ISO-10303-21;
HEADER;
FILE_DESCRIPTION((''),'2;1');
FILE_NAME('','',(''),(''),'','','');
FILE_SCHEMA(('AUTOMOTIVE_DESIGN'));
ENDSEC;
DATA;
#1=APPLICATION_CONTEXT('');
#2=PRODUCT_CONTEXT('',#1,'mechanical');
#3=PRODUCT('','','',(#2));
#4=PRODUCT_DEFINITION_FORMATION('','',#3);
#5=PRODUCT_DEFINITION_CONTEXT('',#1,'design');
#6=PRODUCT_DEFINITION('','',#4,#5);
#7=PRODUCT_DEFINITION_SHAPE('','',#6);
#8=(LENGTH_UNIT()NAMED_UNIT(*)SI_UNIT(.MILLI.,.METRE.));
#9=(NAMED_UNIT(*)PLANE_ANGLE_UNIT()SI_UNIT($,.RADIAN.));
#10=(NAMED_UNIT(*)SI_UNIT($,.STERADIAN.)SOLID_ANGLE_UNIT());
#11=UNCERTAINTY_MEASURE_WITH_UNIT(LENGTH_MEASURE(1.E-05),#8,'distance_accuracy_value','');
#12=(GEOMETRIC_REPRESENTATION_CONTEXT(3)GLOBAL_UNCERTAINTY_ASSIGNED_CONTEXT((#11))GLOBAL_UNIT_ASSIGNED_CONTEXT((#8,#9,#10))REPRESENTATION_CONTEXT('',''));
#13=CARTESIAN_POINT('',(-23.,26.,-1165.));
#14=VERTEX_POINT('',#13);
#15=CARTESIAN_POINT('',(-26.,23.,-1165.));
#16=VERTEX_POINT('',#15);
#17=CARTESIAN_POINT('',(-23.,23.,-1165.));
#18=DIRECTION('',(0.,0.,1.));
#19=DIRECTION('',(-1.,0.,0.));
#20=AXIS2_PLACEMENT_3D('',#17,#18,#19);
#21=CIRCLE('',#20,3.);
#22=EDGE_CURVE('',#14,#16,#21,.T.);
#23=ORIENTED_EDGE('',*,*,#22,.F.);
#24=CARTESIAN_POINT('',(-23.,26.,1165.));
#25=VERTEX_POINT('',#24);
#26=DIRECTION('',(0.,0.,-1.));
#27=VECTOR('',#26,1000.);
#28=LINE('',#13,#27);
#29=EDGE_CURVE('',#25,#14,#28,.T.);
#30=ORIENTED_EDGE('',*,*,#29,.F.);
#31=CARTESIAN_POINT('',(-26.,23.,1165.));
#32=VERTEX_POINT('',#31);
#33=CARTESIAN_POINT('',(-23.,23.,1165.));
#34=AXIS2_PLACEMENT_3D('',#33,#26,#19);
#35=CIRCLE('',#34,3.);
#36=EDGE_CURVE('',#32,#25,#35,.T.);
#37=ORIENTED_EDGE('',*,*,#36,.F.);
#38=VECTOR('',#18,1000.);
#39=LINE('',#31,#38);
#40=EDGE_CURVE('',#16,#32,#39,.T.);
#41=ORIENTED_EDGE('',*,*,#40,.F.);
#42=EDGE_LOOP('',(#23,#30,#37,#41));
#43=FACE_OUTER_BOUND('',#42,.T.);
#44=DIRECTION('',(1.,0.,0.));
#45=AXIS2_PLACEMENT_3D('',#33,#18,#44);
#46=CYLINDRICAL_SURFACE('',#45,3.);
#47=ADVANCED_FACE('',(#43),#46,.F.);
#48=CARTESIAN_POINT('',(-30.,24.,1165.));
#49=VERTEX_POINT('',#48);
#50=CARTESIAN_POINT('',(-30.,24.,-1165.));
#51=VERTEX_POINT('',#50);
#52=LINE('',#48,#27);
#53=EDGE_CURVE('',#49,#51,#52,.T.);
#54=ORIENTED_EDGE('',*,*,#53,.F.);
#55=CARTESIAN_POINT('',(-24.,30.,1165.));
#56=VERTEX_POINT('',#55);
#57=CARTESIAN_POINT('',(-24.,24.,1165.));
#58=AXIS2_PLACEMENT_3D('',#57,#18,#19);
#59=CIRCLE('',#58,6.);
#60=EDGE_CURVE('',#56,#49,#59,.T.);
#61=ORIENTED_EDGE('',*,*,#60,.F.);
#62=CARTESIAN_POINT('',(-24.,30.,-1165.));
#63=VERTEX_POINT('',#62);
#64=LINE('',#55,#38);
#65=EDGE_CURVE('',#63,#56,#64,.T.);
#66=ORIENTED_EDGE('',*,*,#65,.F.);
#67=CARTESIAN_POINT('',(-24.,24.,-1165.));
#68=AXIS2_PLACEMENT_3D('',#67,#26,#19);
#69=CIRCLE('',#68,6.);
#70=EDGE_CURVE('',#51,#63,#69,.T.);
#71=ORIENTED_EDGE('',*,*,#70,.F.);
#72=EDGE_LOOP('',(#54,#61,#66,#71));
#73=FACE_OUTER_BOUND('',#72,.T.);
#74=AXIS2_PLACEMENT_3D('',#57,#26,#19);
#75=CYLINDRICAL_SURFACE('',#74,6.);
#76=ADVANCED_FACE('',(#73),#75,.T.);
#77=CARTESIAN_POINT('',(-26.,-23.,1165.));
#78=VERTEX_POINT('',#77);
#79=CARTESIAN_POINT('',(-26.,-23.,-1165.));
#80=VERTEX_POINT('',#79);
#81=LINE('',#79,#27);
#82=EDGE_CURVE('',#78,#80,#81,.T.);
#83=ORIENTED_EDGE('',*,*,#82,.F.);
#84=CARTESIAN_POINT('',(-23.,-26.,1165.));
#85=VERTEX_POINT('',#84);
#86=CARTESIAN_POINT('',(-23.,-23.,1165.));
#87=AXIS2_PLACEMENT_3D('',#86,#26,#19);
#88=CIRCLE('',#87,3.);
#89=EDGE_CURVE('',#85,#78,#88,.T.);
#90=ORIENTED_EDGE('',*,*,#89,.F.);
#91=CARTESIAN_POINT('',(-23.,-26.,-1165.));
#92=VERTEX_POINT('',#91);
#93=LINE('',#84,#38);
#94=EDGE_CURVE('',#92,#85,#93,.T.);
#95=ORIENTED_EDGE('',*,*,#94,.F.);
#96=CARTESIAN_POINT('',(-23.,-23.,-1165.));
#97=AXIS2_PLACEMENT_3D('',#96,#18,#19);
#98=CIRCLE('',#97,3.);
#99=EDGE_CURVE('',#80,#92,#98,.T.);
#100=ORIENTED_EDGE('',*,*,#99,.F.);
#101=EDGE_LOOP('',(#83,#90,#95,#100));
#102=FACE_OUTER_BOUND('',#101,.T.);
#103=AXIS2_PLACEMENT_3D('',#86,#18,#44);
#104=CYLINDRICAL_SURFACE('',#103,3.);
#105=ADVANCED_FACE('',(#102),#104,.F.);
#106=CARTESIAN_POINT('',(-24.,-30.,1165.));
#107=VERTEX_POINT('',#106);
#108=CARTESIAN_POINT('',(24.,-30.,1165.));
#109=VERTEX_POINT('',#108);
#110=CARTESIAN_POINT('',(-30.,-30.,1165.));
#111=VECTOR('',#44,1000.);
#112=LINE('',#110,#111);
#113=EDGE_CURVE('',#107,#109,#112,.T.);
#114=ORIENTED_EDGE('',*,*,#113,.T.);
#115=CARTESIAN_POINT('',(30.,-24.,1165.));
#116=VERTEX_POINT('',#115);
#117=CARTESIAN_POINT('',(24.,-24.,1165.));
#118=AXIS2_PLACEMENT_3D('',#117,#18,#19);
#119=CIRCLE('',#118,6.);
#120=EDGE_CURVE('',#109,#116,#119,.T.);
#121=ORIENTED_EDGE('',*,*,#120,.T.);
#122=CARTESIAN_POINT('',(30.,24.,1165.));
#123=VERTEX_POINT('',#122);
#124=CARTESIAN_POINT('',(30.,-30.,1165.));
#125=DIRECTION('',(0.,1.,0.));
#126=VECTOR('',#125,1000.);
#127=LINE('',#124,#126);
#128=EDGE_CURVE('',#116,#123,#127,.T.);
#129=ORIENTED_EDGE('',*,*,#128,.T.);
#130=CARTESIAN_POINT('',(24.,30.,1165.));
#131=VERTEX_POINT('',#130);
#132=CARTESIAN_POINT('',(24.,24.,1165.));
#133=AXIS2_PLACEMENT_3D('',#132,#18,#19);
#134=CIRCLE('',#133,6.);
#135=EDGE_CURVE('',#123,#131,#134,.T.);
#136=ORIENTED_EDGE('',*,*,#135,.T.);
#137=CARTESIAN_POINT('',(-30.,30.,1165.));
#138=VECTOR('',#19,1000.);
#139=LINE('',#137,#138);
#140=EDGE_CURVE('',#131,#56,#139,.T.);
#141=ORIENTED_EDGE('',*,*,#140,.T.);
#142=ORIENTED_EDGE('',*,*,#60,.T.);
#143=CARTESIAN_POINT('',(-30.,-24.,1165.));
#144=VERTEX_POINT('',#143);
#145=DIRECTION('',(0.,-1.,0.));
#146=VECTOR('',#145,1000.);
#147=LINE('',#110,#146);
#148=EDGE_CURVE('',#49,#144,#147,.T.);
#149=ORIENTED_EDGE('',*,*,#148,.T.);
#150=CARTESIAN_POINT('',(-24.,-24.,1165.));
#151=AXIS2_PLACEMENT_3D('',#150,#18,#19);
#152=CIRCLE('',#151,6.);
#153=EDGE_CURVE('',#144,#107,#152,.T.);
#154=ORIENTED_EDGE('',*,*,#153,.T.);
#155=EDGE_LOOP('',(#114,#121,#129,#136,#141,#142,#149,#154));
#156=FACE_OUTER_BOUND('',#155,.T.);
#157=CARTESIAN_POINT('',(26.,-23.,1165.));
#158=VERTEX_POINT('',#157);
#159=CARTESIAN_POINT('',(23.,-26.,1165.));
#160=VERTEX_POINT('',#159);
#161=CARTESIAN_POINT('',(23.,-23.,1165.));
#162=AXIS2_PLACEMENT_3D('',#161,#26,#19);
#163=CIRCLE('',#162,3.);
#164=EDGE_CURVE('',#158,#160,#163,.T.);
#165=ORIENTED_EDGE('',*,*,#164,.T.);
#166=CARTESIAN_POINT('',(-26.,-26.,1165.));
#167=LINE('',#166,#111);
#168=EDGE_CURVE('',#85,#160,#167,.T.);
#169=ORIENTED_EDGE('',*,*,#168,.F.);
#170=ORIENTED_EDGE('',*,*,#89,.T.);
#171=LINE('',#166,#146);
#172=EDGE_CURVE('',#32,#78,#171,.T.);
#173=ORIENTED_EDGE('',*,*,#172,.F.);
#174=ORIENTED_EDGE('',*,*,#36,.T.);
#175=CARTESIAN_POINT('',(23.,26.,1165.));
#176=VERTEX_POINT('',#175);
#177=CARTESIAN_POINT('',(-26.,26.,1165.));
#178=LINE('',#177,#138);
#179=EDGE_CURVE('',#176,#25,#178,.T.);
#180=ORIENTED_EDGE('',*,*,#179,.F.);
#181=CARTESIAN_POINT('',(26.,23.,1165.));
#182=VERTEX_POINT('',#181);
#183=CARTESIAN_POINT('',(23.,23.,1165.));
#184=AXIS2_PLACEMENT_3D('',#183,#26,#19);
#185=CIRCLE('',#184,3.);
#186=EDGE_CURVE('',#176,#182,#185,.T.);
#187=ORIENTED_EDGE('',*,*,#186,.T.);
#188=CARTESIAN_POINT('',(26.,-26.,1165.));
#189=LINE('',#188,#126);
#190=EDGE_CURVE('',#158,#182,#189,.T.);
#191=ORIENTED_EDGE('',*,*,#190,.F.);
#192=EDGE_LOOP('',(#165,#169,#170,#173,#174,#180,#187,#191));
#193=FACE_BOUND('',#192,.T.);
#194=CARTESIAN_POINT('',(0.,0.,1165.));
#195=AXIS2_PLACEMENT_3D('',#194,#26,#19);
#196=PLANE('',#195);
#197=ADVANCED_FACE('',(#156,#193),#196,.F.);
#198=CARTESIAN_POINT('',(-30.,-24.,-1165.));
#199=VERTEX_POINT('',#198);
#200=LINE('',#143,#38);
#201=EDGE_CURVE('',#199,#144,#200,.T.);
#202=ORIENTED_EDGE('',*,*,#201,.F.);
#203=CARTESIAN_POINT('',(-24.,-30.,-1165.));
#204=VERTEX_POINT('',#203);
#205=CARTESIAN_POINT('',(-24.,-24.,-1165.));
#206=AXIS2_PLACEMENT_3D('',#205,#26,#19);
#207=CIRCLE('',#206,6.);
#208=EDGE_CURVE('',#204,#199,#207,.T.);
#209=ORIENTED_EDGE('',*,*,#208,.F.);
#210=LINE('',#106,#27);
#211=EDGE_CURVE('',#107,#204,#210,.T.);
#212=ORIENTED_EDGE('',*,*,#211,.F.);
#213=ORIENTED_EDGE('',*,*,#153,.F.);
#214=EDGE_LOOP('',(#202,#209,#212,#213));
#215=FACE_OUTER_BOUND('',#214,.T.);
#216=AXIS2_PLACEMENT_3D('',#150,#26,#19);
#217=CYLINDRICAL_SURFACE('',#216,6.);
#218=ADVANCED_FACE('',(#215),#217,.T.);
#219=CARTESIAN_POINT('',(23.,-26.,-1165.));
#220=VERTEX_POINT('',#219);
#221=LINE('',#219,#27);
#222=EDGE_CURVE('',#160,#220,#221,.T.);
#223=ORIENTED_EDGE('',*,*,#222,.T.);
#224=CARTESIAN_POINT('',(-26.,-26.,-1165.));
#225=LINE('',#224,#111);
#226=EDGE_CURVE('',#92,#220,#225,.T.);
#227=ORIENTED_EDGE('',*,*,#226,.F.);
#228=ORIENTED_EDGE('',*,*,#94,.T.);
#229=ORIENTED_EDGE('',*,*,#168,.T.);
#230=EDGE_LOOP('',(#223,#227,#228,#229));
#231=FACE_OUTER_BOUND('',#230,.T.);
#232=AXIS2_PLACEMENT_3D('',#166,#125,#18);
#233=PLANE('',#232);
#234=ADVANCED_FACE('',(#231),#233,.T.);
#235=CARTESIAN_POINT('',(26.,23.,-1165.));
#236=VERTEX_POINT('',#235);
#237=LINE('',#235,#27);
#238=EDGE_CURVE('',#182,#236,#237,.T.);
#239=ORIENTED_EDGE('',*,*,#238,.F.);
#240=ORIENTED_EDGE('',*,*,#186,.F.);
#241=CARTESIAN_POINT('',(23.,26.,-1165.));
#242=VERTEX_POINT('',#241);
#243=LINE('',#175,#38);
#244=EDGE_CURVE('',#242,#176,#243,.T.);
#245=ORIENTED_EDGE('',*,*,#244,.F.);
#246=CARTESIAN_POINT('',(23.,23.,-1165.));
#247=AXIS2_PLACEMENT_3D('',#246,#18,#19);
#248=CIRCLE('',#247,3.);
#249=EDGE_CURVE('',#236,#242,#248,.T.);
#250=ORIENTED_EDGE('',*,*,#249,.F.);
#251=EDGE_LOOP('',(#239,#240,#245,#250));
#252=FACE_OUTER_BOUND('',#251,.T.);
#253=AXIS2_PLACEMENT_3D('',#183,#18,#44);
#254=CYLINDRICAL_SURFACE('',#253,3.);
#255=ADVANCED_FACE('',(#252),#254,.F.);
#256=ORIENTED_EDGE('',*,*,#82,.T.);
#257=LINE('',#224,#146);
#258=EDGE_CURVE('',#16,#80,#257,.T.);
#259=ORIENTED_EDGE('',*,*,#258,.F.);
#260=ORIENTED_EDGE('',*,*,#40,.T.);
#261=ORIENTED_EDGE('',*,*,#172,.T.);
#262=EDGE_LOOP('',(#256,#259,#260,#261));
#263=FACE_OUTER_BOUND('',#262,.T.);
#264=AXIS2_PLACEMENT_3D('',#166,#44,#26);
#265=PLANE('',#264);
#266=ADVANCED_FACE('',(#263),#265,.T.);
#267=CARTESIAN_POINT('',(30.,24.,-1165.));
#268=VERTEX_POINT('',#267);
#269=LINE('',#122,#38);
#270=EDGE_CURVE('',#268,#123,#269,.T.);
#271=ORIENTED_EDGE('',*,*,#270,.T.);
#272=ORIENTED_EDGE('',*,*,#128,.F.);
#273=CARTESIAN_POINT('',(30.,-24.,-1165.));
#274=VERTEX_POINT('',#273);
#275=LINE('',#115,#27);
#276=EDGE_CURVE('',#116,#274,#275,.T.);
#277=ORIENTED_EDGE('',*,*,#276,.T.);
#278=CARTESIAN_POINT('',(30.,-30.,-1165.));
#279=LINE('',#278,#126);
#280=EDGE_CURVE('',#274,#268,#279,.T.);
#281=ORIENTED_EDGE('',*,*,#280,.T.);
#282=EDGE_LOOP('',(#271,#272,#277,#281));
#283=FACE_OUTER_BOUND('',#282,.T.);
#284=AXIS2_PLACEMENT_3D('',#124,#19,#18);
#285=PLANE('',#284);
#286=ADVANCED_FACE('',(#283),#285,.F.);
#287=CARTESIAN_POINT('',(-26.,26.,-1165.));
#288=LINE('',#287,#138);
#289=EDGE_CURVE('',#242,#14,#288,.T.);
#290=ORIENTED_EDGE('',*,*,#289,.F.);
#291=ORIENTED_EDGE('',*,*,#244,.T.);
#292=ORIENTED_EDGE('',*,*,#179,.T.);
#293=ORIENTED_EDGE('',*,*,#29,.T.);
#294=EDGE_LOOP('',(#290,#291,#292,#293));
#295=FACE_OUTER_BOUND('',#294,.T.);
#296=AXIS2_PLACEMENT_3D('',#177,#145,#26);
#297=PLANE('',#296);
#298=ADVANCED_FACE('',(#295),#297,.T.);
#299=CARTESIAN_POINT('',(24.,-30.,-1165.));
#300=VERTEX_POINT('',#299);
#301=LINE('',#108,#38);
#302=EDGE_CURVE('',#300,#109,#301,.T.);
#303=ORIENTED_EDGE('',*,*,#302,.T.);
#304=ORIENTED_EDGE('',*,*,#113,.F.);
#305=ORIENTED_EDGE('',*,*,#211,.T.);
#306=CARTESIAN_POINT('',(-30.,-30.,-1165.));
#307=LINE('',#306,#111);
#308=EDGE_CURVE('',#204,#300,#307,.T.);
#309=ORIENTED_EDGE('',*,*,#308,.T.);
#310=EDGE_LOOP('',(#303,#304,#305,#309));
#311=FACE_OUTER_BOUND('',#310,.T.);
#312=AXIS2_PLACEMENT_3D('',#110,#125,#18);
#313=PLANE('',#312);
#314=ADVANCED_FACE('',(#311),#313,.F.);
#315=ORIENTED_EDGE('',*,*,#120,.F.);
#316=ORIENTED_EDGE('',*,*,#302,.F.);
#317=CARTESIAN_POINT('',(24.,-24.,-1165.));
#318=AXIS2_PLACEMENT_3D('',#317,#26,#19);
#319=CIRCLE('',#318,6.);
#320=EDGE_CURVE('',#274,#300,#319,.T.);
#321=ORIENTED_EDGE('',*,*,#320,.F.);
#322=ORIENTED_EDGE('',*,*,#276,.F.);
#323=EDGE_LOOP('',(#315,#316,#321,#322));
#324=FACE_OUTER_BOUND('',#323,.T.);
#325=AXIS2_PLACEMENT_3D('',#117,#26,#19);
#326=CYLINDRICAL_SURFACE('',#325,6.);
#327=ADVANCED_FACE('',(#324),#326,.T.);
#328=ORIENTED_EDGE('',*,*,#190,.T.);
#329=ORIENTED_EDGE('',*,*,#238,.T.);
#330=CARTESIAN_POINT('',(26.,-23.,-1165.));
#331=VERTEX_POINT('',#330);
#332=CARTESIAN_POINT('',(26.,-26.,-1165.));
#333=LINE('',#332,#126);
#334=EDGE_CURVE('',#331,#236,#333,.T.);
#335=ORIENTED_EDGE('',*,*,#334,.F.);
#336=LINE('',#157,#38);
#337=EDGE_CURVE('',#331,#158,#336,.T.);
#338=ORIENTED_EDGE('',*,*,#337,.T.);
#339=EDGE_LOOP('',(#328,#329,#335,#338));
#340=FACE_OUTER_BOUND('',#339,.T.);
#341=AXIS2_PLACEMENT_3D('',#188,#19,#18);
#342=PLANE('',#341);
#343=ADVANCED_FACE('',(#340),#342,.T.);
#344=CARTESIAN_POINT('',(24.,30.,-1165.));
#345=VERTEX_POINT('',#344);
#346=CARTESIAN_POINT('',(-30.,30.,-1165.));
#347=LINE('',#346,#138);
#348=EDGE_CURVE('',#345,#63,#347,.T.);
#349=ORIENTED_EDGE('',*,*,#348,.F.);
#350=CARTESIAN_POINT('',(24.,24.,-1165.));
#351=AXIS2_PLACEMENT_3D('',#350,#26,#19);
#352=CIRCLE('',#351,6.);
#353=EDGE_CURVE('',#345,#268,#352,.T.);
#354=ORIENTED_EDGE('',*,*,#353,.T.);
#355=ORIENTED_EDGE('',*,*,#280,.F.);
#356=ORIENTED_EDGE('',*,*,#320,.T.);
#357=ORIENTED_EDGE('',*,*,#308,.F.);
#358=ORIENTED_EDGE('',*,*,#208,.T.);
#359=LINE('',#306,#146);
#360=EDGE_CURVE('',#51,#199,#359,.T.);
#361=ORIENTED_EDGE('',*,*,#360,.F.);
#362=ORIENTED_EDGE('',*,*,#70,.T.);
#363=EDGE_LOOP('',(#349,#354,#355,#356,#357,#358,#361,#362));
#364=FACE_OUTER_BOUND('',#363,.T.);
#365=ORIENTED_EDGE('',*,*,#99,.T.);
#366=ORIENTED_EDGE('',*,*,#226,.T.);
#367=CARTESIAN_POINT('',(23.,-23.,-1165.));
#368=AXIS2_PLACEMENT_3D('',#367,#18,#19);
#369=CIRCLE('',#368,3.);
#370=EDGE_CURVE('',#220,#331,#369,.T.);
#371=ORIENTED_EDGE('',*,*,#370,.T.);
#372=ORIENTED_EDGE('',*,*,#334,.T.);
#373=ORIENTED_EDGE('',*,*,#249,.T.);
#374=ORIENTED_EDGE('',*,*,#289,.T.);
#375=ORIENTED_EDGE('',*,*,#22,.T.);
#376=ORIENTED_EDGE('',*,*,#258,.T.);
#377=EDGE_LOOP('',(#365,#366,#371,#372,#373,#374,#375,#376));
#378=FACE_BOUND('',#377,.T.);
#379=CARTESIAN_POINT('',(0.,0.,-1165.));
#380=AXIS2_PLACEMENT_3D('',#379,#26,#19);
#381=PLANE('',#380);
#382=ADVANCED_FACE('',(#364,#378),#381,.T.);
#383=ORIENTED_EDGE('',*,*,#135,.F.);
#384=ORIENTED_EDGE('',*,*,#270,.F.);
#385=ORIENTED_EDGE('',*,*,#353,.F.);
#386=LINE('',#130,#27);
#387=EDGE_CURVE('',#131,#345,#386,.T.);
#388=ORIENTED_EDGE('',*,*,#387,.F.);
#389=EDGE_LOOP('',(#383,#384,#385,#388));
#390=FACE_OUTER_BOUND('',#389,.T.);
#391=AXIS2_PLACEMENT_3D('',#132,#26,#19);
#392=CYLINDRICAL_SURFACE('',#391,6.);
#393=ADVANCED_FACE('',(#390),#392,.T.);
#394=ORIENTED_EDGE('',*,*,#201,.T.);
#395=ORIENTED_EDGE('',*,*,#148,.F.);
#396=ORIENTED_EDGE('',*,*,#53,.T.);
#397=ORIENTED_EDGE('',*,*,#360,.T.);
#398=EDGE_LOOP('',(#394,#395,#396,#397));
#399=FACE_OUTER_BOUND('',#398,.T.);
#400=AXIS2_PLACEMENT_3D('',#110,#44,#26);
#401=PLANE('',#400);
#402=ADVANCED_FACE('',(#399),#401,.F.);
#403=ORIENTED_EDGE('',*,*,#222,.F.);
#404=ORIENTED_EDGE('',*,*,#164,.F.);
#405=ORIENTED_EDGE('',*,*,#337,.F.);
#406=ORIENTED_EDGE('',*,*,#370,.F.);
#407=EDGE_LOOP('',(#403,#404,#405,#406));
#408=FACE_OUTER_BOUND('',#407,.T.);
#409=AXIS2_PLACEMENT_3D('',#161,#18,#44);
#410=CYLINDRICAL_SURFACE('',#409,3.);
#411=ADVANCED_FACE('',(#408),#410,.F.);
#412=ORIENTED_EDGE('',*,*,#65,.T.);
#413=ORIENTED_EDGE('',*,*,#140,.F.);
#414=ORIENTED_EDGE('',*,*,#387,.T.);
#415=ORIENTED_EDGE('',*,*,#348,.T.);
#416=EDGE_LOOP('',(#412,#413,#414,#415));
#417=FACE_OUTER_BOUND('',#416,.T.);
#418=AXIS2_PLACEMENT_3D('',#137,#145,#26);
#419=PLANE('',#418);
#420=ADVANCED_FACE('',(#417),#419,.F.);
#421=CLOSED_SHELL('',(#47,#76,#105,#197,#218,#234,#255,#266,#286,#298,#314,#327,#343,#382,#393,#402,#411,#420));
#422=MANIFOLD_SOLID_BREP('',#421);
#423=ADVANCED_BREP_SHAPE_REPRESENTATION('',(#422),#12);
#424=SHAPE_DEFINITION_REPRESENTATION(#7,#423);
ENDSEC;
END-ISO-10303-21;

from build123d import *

# Parameters (mm, degrees)
SKETCH1_W           = 60
SKETCH1_H           = 60
SKETCH1_W_2         = 52
SKETCH1_H_2         = 52
BOSS_EXTRUDE1_DEPTH = 1165
FILLET1_R           = 6
FILLET2_R           = 3


with BuildPart() as part:
    # Sketch1 → Boss-Extrude1 (new, symmetric)
    with BuildSketch(Plane.XY):
        Rectangle(SKETCH1_W, SKETCH1_H)
        Rectangle(SKETCH1_W_2, SKETCH1_H_2, mode=Mode.SUBTRACT)
    extrude(amount=BOSS_EXTRUDE1_DEPTH, both=True)

    # Fillet1
    fillet1_edges = [part.edges().sort_by_distance(p)[0] for p in [
        (30, -30, 0),
        (-30, -30, 0),
        (-30, 30, 0),
        (30, 30, 0),
    ]]
    fillet(fillet1_edges, radius=FILLET1_R)

    # Fillet2
    fillet2_edges = [part.edges().sort_by_distance(p)[0] for p in [
        (26, -26, 0),
        (26, 26, 0),
        (-26, 26, 0),
        (-26, -26, 0),
    ]]
    fillet(fillet2_edges, radius=FILLET2_R)


solid = part.part
